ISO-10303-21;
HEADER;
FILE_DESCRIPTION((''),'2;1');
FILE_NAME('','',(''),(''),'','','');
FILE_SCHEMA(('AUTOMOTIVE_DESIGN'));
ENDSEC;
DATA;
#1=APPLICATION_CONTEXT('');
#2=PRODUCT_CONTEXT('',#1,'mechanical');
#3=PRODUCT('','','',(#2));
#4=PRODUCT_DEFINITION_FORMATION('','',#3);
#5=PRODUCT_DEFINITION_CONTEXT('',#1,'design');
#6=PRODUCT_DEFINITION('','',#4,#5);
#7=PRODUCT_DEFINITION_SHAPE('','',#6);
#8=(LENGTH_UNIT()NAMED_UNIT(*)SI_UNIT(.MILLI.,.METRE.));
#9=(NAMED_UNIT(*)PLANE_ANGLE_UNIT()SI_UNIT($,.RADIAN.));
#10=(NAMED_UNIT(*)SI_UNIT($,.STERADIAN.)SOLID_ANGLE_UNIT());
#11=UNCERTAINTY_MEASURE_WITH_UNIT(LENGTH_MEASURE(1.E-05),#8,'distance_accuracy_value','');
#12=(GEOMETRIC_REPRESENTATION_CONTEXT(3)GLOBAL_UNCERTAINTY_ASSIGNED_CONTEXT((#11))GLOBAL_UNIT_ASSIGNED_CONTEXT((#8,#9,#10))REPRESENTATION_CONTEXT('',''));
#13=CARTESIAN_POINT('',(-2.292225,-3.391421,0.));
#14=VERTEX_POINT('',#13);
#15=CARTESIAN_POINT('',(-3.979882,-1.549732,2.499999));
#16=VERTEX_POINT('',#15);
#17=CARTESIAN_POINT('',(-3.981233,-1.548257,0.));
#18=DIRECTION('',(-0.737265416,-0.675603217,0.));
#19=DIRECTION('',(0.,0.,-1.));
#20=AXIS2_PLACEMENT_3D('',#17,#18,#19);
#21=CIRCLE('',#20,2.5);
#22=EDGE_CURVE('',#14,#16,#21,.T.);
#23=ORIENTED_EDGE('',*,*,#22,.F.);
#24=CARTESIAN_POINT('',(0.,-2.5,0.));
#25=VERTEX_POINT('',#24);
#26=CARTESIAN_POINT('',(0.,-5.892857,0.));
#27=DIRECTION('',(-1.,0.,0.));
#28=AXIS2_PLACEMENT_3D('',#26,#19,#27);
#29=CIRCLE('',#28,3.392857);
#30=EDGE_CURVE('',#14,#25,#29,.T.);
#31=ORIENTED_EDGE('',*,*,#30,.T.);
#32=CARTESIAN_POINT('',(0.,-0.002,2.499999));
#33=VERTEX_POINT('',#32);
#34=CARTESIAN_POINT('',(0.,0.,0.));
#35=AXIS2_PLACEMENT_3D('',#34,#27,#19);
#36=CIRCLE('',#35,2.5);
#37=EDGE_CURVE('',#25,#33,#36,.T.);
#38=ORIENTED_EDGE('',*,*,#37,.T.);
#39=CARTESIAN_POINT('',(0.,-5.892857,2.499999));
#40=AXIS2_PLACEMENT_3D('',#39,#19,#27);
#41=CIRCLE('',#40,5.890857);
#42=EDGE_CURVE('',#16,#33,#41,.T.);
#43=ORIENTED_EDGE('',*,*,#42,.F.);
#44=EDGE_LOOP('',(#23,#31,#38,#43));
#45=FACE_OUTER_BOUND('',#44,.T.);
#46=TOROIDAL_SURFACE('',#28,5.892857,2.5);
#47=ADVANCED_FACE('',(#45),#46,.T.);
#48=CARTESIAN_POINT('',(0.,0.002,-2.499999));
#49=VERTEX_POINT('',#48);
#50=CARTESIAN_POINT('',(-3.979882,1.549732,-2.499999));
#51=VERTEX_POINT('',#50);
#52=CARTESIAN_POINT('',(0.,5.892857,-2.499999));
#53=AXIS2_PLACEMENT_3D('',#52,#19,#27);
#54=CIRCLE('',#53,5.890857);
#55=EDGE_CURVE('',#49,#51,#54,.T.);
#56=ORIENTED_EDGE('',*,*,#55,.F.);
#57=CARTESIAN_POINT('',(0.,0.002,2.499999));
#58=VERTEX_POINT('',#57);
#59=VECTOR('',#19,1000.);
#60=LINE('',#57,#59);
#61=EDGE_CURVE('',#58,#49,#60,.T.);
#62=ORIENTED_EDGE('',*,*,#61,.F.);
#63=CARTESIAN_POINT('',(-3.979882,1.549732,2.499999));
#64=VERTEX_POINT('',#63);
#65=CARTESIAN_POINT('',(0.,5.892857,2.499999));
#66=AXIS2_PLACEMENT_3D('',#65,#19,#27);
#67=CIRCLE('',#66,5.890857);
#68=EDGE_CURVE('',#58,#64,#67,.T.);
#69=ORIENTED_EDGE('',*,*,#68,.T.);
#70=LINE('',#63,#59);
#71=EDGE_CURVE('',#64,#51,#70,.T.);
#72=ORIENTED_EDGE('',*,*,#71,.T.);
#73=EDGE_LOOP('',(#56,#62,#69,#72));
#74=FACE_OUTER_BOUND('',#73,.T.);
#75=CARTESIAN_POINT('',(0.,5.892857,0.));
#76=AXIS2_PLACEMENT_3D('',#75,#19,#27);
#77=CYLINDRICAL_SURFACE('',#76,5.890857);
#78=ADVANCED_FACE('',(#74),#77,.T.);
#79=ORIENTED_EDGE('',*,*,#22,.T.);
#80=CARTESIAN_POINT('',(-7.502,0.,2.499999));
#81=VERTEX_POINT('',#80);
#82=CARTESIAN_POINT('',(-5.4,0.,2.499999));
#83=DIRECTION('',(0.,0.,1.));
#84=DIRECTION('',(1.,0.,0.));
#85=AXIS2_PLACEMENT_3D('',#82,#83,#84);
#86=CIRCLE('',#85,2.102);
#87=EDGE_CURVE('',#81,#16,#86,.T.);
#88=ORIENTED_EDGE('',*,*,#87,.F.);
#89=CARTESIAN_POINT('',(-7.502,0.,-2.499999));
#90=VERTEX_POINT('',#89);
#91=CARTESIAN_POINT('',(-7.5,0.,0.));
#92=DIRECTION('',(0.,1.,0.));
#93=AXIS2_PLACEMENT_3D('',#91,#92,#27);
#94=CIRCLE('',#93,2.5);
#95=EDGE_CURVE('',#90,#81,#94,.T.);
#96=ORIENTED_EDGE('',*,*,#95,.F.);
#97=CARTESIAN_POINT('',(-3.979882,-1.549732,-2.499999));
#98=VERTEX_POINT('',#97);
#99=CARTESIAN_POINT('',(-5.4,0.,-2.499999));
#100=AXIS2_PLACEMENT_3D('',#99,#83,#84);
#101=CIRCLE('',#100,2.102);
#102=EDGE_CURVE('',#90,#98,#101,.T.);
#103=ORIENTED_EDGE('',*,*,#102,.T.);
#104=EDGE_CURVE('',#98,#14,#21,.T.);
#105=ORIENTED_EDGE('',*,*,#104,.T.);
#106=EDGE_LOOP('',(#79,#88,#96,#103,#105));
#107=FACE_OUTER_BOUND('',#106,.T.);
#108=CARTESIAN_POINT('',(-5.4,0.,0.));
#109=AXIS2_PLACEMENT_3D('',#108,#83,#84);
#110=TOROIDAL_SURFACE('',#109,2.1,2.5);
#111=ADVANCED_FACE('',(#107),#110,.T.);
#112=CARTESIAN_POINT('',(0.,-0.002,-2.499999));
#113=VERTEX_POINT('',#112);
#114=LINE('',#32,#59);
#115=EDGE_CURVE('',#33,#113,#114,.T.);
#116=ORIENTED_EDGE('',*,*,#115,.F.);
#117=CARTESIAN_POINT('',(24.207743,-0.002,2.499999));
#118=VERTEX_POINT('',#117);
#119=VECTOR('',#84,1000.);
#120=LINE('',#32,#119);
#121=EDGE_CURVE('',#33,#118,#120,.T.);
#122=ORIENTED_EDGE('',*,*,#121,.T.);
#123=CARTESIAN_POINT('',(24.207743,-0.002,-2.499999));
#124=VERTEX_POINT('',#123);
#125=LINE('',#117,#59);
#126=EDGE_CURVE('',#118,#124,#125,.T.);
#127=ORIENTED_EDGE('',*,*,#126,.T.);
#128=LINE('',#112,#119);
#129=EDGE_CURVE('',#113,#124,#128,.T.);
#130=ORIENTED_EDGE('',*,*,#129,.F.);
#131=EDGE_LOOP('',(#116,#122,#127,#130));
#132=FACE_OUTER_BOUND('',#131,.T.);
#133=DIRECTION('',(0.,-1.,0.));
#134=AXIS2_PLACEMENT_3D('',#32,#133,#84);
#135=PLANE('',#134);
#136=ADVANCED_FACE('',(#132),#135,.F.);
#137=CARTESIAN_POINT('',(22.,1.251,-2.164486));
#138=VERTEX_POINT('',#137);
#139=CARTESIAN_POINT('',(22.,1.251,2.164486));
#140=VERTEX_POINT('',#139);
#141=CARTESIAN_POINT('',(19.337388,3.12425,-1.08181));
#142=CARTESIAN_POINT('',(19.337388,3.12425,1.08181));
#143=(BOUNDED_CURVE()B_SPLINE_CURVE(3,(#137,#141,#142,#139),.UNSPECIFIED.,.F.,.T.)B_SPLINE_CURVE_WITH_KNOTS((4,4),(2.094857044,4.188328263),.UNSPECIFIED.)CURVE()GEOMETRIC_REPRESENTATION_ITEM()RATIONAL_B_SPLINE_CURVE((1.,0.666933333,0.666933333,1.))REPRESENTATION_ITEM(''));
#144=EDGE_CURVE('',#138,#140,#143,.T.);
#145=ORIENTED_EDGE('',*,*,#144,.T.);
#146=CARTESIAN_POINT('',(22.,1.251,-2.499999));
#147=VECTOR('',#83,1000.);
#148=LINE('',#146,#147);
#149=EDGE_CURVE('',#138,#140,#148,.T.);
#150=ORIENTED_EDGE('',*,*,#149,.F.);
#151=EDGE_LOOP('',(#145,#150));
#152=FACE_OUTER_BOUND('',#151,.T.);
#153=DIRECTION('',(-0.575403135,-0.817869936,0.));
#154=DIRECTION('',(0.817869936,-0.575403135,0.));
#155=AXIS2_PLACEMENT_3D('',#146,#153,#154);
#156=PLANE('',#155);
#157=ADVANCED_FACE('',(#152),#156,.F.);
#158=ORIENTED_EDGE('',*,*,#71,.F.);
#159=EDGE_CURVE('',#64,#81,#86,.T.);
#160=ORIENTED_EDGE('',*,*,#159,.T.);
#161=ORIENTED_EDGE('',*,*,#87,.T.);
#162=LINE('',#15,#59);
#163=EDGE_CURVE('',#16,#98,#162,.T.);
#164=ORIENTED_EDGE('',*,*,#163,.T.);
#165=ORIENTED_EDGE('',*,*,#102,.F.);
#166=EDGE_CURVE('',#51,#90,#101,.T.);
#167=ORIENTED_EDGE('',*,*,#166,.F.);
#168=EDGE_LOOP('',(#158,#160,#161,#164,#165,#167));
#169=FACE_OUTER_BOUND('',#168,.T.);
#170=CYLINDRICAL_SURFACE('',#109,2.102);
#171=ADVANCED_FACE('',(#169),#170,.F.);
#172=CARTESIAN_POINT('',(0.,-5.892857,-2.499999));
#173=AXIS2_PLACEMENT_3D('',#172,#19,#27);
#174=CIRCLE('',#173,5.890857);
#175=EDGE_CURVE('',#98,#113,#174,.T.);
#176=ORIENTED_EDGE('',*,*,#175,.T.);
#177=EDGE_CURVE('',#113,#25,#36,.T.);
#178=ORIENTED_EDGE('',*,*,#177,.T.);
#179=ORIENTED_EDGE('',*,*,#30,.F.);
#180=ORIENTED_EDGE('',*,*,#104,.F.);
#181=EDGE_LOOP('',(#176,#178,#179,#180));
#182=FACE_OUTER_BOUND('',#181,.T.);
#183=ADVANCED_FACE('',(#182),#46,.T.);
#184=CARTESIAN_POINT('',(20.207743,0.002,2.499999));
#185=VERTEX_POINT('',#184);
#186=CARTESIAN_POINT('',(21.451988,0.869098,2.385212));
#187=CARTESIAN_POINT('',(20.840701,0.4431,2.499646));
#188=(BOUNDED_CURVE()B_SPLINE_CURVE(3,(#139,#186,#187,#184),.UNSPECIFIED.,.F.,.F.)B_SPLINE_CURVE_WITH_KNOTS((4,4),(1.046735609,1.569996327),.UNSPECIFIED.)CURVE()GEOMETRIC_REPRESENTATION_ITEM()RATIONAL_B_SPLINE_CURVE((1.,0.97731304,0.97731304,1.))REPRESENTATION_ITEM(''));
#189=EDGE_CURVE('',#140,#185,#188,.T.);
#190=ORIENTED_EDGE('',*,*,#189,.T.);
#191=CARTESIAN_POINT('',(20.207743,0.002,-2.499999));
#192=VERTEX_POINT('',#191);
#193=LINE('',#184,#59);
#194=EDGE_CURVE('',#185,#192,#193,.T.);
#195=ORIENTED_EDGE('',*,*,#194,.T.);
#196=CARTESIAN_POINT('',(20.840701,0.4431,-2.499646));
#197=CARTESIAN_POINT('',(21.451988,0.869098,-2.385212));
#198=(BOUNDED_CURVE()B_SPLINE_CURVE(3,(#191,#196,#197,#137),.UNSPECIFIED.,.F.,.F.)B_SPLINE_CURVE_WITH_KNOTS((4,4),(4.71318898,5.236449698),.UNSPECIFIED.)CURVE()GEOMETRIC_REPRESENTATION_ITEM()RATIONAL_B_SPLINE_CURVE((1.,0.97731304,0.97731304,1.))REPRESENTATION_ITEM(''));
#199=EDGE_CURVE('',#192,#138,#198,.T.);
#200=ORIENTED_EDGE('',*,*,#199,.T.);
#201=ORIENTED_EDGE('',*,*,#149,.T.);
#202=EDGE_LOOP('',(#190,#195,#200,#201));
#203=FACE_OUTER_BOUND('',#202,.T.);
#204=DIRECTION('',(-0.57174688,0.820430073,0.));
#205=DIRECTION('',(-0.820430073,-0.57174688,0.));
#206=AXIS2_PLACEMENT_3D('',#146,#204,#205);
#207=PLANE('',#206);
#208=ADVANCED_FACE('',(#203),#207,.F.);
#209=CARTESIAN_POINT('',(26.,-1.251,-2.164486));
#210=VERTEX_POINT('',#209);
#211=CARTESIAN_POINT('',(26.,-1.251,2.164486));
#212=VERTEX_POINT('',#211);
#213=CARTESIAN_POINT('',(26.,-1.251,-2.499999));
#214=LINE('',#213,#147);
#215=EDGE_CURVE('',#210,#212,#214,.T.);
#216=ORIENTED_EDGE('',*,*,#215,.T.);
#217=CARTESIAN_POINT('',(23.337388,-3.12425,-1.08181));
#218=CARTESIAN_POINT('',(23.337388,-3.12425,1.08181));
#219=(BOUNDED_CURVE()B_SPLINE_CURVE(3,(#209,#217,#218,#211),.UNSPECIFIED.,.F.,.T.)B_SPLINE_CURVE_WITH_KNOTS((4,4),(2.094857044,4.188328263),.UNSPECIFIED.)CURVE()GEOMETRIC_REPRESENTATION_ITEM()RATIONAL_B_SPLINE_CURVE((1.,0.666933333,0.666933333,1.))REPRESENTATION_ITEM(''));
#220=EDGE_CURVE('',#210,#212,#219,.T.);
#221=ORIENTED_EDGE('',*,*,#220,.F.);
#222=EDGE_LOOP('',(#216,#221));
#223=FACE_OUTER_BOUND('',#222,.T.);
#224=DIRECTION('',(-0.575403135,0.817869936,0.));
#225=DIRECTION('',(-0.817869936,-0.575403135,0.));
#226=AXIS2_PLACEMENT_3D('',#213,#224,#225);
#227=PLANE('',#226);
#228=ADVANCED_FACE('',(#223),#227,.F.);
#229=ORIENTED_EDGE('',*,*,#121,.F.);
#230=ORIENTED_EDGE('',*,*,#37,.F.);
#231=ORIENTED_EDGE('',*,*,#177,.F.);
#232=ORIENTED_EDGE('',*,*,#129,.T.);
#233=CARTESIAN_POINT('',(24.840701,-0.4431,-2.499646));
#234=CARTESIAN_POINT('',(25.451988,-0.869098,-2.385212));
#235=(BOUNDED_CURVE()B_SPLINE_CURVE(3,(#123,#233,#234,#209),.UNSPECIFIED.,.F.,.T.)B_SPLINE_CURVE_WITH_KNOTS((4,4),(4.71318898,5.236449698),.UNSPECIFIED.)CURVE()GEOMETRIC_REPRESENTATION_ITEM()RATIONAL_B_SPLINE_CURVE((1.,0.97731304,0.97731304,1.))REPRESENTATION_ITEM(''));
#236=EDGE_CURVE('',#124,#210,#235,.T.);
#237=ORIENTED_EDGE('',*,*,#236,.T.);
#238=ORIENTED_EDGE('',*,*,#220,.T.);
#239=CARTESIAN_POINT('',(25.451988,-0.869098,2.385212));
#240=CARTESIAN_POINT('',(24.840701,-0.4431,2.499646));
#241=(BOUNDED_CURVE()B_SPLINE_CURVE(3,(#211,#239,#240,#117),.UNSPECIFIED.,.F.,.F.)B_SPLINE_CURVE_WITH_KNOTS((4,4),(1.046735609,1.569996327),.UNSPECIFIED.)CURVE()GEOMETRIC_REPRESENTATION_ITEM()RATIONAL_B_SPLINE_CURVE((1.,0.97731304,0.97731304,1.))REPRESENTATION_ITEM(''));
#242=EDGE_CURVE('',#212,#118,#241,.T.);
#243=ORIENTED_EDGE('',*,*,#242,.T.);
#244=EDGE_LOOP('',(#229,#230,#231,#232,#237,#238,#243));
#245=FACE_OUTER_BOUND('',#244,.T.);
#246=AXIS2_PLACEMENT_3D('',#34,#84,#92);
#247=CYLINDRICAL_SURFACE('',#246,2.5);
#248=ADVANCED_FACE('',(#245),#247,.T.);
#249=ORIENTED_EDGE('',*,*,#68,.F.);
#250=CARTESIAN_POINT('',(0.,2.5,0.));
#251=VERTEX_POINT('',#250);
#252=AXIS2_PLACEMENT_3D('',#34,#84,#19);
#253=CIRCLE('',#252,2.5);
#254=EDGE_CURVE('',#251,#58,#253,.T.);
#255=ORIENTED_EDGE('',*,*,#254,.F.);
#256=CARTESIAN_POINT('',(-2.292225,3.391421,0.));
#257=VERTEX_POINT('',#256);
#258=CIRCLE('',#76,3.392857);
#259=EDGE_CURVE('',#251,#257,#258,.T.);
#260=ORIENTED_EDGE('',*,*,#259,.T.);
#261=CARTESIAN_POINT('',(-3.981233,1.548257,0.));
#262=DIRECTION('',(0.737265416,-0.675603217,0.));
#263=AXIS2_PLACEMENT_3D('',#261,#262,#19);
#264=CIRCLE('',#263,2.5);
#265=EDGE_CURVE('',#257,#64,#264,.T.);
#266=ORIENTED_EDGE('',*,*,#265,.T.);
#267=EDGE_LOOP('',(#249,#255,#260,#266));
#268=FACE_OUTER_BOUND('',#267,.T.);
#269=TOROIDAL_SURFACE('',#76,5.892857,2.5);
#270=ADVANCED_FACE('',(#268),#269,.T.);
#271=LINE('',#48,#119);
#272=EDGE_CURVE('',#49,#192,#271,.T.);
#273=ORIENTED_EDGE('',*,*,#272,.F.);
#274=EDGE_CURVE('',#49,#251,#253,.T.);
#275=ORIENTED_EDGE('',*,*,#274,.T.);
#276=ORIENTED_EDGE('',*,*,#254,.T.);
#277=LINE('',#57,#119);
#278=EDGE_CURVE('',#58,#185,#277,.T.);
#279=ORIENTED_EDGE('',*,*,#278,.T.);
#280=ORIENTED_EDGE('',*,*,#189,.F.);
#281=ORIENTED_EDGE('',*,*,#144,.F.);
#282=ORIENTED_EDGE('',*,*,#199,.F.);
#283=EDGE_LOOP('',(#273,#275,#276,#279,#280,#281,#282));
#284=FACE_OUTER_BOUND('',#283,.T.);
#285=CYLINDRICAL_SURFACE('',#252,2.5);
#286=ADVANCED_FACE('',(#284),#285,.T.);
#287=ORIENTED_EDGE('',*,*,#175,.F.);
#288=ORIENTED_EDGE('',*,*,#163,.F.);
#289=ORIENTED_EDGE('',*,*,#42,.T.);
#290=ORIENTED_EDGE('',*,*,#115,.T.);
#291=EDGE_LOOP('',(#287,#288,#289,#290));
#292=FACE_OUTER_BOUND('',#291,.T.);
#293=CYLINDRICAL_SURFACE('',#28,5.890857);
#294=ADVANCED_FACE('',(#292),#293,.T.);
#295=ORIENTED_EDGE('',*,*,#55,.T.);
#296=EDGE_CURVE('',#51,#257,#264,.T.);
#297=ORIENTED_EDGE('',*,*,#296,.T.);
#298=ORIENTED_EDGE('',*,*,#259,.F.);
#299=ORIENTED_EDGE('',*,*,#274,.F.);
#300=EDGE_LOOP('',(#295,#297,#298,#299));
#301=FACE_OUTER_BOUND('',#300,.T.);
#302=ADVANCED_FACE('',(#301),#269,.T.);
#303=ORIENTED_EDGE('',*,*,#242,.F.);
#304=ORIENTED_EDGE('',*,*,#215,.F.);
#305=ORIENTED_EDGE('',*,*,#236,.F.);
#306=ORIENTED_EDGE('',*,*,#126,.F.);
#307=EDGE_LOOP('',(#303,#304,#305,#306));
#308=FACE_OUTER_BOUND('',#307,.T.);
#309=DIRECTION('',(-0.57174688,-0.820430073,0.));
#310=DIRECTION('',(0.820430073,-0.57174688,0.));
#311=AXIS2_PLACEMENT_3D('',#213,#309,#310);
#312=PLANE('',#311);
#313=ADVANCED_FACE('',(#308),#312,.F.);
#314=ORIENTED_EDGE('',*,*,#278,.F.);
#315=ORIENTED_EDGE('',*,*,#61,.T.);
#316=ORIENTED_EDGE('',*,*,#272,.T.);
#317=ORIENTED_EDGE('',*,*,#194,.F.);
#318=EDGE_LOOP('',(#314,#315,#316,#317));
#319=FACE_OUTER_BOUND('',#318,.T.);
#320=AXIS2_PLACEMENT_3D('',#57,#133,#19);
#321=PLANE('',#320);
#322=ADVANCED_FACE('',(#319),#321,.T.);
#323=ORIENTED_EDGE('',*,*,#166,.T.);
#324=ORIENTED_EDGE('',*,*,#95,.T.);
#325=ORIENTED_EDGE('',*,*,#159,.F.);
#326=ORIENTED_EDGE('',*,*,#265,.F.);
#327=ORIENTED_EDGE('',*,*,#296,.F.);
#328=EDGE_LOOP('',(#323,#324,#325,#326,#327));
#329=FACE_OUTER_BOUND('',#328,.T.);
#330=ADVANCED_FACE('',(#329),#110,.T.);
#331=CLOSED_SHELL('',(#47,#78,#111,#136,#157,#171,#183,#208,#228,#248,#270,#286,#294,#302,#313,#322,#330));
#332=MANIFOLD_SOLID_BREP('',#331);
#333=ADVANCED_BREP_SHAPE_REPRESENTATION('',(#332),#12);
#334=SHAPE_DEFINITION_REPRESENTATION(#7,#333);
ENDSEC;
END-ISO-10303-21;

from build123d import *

# Parameters (mm, degrees)
CONECUT_DEPTH      = 27.521877713
CONECUT_DEPTH_BACK = 27.521877713


with BuildPart() as part:
    # Body: sweep along a path in Sketch2
    with BuildLine(Plane.XY) as body_path:
        Line((22, 2.5), (0, 2.5))
        ThreePointArc((0, 2.5), (-1.229728386, 2.730698436), (-2.292225201, 3.391420912))
        ThreePointArc((-2.292225201, 3.391420912), (-10, 0), (-2.292225201, -3.391420912))
        ThreePointArc((-2.292225201, -3.391420912), (-1.229728386, -2.730698436), (0, -2.5))
        Line((0, -2.5), (26, -2.5))
    # Sketch1 → Body (sweep)
    with BuildSketch(Plane(origin=(22, 0, 0), x_dir=(0, 0, -1), z_dir=(1, 0, 0))):
        with BuildLine():
            Line((-2.4999992, 0.002), (2.4999992, 0.002))
            ThreePointArc((2.4999992, 0.002), (0, 2.5), (-2.4999992, 0.002))
        make_face()
    sweep(path=body_path.line)

    # Sketch3 → ConeCut (cut, two sides: drawn at the far end of the back side and taken through both)
    with BuildSketch(Plane.XY.offset(-CONECUT_DEPTH_BACK)):
        Polygon((22, 1.251), (20.210475082, 2.51), (26.01, 2.51), (26.01, -2.51), (24.210475082, -2.51), (26, -1.251), (24.204873421, 0), (20.204873421, 0), align=None)
    extrude(amount=CONECUT_DEPTH + CONECUT_DEPTH_BACK, mode=Mode.SUBTRACT)


solid = part.part
